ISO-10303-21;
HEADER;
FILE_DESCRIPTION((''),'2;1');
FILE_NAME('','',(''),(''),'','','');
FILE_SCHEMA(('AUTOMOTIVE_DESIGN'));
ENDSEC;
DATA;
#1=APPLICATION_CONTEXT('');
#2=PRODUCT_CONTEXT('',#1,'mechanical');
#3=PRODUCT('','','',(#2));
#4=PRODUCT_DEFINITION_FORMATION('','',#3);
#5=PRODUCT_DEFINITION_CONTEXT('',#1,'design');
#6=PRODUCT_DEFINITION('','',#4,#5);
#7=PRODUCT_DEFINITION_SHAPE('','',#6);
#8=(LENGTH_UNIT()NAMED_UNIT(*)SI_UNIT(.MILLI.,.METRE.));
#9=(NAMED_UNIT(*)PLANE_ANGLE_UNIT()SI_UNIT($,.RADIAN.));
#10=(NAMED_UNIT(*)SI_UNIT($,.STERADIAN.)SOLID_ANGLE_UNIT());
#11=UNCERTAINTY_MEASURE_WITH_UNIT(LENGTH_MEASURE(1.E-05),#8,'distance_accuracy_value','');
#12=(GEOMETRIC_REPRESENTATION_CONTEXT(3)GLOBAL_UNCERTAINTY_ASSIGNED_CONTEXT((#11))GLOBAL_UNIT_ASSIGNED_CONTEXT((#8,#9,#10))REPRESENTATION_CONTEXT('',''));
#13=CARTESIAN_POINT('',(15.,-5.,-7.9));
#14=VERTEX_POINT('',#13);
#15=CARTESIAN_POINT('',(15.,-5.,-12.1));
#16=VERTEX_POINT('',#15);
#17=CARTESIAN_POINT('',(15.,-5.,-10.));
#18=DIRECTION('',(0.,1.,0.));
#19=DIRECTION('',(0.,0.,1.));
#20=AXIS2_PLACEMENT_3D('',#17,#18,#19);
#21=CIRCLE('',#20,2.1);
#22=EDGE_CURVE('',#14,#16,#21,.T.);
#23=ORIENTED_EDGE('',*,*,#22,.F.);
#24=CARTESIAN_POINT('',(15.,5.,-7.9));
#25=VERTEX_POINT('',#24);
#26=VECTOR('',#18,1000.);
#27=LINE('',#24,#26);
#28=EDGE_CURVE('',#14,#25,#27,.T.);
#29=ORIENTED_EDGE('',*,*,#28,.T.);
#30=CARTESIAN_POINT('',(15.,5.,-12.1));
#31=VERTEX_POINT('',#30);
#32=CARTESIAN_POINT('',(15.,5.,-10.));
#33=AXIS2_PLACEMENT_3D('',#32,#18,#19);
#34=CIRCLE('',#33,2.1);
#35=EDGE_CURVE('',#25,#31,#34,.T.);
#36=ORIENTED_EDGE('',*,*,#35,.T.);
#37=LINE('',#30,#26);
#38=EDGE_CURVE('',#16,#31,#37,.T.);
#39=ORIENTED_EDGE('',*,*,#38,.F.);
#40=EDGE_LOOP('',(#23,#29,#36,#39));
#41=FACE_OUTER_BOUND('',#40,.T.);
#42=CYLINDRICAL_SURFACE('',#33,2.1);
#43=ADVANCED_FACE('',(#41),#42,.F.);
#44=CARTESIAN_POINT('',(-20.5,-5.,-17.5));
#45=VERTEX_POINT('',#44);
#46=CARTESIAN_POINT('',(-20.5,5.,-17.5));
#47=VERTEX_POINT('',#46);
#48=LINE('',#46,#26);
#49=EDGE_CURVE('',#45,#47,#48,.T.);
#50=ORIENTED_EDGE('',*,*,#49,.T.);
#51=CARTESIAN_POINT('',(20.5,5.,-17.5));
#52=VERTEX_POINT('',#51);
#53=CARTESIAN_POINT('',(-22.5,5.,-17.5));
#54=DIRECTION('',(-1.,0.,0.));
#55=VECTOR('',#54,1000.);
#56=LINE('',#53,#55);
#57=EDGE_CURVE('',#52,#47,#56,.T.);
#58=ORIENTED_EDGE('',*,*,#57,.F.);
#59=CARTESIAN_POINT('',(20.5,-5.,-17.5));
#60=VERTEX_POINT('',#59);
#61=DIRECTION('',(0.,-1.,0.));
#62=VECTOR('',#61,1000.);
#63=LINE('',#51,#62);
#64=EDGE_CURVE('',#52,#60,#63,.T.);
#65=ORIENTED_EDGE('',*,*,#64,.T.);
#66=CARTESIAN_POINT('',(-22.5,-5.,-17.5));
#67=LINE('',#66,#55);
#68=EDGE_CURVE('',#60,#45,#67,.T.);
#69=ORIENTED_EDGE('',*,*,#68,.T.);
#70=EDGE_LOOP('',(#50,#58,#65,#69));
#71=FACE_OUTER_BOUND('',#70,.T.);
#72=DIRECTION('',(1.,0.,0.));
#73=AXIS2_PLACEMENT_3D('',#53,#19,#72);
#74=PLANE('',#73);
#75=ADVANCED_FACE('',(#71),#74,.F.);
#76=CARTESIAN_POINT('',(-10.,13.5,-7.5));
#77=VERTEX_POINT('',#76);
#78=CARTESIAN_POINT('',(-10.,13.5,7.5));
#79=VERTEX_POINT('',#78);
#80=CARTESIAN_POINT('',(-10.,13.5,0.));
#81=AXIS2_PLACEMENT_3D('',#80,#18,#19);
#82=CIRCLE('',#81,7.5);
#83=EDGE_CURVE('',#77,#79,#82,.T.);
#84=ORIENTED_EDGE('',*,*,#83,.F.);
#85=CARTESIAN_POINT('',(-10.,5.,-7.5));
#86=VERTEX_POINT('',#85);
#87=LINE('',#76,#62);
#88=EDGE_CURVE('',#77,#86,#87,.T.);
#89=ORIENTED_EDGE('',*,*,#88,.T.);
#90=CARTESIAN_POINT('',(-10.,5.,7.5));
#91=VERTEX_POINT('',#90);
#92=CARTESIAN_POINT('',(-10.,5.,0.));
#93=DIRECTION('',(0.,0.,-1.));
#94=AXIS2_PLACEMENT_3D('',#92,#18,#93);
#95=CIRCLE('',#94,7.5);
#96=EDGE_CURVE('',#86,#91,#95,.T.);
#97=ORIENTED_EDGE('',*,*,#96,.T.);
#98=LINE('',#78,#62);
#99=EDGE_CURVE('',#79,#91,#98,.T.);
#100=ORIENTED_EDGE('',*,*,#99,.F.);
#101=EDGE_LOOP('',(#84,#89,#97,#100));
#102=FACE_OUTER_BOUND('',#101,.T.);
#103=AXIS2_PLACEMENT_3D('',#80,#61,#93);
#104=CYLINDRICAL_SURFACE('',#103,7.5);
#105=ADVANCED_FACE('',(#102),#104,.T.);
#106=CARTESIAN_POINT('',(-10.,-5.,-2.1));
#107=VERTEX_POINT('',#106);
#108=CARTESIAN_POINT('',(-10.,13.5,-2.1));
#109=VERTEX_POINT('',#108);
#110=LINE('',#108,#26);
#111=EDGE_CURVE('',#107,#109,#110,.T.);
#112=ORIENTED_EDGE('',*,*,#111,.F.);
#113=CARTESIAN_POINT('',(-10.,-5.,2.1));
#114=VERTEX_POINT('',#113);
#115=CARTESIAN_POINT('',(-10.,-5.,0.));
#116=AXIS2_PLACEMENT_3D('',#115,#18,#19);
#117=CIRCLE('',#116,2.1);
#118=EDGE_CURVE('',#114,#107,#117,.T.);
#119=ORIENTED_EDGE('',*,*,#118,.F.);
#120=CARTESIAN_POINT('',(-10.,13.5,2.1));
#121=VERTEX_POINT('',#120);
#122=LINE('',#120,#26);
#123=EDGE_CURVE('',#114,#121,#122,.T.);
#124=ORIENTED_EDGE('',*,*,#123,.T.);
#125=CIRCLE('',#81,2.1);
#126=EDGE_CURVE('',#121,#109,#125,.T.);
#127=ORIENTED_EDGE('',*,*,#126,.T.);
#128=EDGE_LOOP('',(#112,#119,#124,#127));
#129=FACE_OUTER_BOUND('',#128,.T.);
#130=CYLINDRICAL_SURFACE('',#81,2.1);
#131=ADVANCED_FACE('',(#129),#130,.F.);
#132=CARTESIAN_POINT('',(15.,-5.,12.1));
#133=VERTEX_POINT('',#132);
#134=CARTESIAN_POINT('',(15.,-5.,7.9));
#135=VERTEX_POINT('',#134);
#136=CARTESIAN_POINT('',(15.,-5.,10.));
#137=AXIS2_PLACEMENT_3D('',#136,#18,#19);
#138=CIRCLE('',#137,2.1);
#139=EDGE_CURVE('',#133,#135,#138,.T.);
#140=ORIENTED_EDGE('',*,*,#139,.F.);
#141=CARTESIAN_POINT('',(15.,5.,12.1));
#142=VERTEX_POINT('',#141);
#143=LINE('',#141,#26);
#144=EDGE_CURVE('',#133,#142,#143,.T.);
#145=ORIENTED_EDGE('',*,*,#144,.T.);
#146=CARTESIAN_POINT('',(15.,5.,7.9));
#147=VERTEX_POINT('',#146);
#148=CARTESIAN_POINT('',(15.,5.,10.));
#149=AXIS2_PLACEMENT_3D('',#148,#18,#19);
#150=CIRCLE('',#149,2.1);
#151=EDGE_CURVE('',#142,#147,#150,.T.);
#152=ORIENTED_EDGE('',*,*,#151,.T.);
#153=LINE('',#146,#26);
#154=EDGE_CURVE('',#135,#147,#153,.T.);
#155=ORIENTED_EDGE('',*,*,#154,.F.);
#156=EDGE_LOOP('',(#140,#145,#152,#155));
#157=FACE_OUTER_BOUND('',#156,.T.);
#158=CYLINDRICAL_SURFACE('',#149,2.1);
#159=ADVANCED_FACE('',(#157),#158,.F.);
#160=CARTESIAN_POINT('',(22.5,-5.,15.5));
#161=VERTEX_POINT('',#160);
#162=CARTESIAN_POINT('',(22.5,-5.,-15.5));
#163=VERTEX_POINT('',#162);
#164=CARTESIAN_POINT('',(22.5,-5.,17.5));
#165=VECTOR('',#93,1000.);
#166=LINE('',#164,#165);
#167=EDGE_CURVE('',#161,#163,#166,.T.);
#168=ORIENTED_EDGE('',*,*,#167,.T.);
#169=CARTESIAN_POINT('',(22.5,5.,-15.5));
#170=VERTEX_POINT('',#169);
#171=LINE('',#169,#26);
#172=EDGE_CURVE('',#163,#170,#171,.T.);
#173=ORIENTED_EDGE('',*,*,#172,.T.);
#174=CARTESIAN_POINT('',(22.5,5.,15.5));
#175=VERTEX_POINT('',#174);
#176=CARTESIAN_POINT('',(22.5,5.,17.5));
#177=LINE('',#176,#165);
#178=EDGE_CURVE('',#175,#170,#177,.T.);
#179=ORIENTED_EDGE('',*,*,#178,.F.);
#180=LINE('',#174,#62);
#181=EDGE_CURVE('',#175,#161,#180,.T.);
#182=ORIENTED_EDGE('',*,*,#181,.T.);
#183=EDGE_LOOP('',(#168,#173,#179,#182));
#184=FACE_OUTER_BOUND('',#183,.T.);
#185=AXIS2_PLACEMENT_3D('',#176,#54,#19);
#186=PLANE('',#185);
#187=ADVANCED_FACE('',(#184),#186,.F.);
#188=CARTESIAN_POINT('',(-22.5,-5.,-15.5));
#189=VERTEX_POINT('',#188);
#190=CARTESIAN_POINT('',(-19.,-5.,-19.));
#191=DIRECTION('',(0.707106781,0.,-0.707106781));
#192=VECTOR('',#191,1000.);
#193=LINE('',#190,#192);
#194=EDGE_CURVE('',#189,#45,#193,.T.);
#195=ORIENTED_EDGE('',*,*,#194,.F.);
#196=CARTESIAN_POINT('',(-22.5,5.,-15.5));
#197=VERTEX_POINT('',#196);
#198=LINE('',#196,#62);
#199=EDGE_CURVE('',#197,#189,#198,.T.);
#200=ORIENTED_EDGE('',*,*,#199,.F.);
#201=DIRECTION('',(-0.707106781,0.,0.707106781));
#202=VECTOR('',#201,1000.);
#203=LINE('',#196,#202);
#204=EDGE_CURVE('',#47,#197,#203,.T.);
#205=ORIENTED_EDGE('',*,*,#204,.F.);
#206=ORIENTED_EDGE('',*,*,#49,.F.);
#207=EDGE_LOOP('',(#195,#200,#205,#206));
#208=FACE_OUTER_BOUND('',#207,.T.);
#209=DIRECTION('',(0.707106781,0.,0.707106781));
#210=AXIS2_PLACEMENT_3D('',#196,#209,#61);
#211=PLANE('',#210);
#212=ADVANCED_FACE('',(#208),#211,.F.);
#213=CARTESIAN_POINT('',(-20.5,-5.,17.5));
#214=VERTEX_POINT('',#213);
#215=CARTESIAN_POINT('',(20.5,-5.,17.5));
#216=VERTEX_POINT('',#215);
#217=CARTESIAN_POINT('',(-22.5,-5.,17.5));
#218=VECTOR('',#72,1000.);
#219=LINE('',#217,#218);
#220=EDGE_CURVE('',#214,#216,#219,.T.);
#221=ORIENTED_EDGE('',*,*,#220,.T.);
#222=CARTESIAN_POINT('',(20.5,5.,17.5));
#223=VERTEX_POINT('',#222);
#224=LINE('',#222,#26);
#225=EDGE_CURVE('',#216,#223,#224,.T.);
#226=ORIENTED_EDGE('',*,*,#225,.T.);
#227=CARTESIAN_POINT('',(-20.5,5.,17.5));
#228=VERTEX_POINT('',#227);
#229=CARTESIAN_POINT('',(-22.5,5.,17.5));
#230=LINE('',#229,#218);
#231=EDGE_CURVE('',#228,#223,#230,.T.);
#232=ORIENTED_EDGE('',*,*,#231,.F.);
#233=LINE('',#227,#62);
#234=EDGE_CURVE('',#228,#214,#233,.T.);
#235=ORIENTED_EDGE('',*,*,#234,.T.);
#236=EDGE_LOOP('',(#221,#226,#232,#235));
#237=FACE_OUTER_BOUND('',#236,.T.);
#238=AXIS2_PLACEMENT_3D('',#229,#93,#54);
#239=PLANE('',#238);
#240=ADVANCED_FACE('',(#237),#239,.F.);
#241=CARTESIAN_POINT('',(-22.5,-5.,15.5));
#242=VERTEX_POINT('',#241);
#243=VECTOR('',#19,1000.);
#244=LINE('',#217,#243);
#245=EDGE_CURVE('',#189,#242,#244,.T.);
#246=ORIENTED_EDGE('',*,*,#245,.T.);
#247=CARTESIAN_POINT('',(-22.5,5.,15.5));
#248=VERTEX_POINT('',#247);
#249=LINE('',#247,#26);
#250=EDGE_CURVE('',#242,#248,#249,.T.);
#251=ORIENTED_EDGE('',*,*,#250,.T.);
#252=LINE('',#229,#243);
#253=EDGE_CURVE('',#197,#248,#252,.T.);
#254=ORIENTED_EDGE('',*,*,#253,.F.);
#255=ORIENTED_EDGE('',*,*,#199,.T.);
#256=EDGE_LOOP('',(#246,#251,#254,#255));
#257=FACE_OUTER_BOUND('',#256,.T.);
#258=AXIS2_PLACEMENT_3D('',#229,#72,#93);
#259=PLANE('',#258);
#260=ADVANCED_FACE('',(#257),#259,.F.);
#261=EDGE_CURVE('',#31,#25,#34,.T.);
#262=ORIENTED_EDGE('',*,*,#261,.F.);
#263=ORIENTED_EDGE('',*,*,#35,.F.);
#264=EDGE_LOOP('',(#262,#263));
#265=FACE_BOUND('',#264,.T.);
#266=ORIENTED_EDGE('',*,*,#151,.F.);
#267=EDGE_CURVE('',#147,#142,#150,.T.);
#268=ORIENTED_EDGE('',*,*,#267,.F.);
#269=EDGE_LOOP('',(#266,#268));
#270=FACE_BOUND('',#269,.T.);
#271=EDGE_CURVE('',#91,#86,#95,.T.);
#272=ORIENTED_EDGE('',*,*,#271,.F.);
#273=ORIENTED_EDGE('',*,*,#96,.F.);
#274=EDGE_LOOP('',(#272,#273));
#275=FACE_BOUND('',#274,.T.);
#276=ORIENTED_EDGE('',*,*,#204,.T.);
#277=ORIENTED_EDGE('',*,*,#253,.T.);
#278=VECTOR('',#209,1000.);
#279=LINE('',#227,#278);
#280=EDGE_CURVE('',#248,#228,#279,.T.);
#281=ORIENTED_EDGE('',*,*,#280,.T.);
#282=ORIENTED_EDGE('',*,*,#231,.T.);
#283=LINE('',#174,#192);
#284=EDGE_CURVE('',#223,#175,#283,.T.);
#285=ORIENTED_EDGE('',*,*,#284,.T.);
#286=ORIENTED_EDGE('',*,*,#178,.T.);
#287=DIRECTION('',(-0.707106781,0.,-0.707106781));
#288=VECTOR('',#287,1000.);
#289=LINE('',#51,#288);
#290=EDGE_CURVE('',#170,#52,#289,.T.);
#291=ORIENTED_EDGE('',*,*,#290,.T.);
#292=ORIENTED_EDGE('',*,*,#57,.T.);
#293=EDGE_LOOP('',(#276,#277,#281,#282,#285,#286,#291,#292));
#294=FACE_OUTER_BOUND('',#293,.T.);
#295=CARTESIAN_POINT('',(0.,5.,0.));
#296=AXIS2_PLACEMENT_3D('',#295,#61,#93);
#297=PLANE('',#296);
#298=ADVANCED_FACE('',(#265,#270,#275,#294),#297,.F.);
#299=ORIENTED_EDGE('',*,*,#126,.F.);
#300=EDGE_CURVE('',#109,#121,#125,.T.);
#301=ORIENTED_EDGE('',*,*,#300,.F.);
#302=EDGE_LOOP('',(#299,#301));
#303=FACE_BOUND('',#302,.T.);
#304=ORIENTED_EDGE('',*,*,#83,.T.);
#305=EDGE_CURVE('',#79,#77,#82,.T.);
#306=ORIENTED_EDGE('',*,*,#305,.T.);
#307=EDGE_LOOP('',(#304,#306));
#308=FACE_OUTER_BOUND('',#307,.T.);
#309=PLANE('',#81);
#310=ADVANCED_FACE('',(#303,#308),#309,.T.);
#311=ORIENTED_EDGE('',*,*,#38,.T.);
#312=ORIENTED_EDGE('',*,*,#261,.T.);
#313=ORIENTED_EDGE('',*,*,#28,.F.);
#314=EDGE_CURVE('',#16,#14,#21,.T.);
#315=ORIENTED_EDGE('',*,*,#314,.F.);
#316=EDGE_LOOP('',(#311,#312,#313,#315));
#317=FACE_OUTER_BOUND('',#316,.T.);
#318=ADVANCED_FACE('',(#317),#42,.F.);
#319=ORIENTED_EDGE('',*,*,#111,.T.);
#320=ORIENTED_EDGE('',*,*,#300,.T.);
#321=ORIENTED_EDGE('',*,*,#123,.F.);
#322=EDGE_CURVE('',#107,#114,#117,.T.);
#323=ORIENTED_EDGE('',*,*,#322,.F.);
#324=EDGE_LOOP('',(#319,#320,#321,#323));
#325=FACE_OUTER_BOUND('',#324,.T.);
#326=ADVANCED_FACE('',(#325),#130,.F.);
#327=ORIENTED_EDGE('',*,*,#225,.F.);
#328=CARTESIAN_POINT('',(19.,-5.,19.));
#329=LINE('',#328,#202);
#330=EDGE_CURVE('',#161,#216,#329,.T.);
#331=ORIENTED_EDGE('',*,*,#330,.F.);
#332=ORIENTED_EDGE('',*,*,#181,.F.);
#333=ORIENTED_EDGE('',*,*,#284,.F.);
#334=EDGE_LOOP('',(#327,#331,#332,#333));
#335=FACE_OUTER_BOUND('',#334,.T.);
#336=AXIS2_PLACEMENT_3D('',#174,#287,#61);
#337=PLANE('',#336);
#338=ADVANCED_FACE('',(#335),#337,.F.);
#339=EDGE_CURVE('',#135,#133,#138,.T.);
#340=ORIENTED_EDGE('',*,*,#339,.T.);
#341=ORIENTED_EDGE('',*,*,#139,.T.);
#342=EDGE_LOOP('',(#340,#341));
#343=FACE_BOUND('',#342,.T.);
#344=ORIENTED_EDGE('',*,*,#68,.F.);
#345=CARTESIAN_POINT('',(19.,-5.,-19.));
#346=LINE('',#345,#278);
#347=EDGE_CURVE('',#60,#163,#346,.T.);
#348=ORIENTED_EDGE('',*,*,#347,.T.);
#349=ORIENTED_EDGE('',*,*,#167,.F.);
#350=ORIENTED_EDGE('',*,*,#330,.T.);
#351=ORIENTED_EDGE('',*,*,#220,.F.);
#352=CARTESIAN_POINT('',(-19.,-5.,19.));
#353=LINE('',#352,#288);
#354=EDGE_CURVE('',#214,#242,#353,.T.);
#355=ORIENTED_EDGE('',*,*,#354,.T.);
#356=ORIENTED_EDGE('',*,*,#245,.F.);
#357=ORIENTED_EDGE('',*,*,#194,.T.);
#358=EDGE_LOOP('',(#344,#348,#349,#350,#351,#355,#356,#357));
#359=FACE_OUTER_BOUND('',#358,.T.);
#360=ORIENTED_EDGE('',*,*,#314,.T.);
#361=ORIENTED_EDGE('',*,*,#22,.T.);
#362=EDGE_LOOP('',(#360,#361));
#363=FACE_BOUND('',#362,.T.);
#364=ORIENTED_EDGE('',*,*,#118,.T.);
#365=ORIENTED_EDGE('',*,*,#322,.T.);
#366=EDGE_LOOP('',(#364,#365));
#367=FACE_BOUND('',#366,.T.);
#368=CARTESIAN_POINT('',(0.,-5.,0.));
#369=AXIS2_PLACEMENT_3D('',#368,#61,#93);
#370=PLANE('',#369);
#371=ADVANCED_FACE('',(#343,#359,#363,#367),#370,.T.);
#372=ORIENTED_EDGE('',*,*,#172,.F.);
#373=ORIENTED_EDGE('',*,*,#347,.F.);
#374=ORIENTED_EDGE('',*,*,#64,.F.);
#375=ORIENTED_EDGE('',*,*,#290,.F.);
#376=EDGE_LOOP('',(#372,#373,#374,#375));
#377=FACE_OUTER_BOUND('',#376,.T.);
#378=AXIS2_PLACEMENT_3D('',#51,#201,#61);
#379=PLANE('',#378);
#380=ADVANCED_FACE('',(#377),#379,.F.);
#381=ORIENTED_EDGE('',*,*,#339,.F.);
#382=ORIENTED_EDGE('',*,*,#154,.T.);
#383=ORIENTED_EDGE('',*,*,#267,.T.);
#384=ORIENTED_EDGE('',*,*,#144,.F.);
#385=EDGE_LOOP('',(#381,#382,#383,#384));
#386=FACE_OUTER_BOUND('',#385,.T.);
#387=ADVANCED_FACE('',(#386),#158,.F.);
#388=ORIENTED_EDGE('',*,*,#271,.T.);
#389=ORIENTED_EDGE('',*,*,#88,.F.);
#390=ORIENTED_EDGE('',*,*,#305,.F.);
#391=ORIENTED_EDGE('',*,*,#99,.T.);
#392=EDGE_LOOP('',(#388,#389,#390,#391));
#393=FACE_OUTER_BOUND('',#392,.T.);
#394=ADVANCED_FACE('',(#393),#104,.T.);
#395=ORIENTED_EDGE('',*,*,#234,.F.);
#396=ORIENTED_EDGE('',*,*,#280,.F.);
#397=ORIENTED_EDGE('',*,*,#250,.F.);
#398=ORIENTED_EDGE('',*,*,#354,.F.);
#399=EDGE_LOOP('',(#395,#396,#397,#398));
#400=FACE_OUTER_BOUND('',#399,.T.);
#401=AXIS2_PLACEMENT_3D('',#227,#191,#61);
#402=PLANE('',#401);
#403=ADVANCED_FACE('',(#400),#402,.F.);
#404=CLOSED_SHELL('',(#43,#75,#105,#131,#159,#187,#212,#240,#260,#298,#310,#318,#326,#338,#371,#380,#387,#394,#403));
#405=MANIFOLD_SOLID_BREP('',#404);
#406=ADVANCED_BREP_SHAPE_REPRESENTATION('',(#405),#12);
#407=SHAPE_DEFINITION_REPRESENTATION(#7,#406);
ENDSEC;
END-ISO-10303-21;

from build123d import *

# Parameters (mm, degrees)
SKETCH_1_W         = 45
SKETCH_1_H         = 35
EXTRUDE_1_DEPTH    = 5
CHAMFER_1_SIZE     = 2
SKETCH_8_R         = 7.5
EXTRUDE_2_DEPTH    = 8.5
HOLE_WIZARD_M5_1_D = 4.2
HOLE_WIZARD_M5_2_D = 4.2


with BuildPart() as part:
    # 草图1 → 凸台-拉伸1 (new, symmetric)
    with BuildSketch(Plane(origin=(0, 0, 0), x_dir=(1, 0, 0), z_dir=(0, 1, 0))):
        Rectangle(SKETCH_1_W, SKETCH_1_H)
    extrude(amount=EXTRUDE_1_DEPTH, both=True)

    # 倒角1
    chamfer_1_edges = [part.edges().sort_by_distance(p)[0] for p in [
        (22.5, 0, 17.5),
        (-22.5, 0, 17.5),
        (-22.5, 0, -17.5),
        (22.5, 0, -17.5),
    ]]
    chamfer(chamfer_1_edges, length=CHAMFER_1_SIZE)

    # 草图8 → 凸台-拉伸2 (add)
    with BuildSketch(Plane(origin=(0, 5, 0), x_dir=(1, 0, 0), z_dir=(0, 1, 0))):
        with Locations(Location((-10, 0, 0), (0, 0, 90))):
            Circle(SKETCH_8_R)
    extrude(amount=EXTRUDE_2_DEPTH)

    # M5 螺纹孔1 (through all)
    with Locations(Plane(origin=(0, 5, 0), x_dir=(1, 0, 0), z_dir=(0, 1, 0))):
        with Locations((15, -10), (15, 10)):
            Hole(HOLE_WIZARD_M5_1_D / 2)

    # M5 螺纹孔2 (through all)
    with Locations(Plane(origin=(0, 13.5, 0), x_dir=(1, 0, 0), z_dir=(0, 1, 0))):
        with Locations((-10, 0)):
            Hole(HOLE_WIZARD_M5_2_D / 2)


solid = part.part
